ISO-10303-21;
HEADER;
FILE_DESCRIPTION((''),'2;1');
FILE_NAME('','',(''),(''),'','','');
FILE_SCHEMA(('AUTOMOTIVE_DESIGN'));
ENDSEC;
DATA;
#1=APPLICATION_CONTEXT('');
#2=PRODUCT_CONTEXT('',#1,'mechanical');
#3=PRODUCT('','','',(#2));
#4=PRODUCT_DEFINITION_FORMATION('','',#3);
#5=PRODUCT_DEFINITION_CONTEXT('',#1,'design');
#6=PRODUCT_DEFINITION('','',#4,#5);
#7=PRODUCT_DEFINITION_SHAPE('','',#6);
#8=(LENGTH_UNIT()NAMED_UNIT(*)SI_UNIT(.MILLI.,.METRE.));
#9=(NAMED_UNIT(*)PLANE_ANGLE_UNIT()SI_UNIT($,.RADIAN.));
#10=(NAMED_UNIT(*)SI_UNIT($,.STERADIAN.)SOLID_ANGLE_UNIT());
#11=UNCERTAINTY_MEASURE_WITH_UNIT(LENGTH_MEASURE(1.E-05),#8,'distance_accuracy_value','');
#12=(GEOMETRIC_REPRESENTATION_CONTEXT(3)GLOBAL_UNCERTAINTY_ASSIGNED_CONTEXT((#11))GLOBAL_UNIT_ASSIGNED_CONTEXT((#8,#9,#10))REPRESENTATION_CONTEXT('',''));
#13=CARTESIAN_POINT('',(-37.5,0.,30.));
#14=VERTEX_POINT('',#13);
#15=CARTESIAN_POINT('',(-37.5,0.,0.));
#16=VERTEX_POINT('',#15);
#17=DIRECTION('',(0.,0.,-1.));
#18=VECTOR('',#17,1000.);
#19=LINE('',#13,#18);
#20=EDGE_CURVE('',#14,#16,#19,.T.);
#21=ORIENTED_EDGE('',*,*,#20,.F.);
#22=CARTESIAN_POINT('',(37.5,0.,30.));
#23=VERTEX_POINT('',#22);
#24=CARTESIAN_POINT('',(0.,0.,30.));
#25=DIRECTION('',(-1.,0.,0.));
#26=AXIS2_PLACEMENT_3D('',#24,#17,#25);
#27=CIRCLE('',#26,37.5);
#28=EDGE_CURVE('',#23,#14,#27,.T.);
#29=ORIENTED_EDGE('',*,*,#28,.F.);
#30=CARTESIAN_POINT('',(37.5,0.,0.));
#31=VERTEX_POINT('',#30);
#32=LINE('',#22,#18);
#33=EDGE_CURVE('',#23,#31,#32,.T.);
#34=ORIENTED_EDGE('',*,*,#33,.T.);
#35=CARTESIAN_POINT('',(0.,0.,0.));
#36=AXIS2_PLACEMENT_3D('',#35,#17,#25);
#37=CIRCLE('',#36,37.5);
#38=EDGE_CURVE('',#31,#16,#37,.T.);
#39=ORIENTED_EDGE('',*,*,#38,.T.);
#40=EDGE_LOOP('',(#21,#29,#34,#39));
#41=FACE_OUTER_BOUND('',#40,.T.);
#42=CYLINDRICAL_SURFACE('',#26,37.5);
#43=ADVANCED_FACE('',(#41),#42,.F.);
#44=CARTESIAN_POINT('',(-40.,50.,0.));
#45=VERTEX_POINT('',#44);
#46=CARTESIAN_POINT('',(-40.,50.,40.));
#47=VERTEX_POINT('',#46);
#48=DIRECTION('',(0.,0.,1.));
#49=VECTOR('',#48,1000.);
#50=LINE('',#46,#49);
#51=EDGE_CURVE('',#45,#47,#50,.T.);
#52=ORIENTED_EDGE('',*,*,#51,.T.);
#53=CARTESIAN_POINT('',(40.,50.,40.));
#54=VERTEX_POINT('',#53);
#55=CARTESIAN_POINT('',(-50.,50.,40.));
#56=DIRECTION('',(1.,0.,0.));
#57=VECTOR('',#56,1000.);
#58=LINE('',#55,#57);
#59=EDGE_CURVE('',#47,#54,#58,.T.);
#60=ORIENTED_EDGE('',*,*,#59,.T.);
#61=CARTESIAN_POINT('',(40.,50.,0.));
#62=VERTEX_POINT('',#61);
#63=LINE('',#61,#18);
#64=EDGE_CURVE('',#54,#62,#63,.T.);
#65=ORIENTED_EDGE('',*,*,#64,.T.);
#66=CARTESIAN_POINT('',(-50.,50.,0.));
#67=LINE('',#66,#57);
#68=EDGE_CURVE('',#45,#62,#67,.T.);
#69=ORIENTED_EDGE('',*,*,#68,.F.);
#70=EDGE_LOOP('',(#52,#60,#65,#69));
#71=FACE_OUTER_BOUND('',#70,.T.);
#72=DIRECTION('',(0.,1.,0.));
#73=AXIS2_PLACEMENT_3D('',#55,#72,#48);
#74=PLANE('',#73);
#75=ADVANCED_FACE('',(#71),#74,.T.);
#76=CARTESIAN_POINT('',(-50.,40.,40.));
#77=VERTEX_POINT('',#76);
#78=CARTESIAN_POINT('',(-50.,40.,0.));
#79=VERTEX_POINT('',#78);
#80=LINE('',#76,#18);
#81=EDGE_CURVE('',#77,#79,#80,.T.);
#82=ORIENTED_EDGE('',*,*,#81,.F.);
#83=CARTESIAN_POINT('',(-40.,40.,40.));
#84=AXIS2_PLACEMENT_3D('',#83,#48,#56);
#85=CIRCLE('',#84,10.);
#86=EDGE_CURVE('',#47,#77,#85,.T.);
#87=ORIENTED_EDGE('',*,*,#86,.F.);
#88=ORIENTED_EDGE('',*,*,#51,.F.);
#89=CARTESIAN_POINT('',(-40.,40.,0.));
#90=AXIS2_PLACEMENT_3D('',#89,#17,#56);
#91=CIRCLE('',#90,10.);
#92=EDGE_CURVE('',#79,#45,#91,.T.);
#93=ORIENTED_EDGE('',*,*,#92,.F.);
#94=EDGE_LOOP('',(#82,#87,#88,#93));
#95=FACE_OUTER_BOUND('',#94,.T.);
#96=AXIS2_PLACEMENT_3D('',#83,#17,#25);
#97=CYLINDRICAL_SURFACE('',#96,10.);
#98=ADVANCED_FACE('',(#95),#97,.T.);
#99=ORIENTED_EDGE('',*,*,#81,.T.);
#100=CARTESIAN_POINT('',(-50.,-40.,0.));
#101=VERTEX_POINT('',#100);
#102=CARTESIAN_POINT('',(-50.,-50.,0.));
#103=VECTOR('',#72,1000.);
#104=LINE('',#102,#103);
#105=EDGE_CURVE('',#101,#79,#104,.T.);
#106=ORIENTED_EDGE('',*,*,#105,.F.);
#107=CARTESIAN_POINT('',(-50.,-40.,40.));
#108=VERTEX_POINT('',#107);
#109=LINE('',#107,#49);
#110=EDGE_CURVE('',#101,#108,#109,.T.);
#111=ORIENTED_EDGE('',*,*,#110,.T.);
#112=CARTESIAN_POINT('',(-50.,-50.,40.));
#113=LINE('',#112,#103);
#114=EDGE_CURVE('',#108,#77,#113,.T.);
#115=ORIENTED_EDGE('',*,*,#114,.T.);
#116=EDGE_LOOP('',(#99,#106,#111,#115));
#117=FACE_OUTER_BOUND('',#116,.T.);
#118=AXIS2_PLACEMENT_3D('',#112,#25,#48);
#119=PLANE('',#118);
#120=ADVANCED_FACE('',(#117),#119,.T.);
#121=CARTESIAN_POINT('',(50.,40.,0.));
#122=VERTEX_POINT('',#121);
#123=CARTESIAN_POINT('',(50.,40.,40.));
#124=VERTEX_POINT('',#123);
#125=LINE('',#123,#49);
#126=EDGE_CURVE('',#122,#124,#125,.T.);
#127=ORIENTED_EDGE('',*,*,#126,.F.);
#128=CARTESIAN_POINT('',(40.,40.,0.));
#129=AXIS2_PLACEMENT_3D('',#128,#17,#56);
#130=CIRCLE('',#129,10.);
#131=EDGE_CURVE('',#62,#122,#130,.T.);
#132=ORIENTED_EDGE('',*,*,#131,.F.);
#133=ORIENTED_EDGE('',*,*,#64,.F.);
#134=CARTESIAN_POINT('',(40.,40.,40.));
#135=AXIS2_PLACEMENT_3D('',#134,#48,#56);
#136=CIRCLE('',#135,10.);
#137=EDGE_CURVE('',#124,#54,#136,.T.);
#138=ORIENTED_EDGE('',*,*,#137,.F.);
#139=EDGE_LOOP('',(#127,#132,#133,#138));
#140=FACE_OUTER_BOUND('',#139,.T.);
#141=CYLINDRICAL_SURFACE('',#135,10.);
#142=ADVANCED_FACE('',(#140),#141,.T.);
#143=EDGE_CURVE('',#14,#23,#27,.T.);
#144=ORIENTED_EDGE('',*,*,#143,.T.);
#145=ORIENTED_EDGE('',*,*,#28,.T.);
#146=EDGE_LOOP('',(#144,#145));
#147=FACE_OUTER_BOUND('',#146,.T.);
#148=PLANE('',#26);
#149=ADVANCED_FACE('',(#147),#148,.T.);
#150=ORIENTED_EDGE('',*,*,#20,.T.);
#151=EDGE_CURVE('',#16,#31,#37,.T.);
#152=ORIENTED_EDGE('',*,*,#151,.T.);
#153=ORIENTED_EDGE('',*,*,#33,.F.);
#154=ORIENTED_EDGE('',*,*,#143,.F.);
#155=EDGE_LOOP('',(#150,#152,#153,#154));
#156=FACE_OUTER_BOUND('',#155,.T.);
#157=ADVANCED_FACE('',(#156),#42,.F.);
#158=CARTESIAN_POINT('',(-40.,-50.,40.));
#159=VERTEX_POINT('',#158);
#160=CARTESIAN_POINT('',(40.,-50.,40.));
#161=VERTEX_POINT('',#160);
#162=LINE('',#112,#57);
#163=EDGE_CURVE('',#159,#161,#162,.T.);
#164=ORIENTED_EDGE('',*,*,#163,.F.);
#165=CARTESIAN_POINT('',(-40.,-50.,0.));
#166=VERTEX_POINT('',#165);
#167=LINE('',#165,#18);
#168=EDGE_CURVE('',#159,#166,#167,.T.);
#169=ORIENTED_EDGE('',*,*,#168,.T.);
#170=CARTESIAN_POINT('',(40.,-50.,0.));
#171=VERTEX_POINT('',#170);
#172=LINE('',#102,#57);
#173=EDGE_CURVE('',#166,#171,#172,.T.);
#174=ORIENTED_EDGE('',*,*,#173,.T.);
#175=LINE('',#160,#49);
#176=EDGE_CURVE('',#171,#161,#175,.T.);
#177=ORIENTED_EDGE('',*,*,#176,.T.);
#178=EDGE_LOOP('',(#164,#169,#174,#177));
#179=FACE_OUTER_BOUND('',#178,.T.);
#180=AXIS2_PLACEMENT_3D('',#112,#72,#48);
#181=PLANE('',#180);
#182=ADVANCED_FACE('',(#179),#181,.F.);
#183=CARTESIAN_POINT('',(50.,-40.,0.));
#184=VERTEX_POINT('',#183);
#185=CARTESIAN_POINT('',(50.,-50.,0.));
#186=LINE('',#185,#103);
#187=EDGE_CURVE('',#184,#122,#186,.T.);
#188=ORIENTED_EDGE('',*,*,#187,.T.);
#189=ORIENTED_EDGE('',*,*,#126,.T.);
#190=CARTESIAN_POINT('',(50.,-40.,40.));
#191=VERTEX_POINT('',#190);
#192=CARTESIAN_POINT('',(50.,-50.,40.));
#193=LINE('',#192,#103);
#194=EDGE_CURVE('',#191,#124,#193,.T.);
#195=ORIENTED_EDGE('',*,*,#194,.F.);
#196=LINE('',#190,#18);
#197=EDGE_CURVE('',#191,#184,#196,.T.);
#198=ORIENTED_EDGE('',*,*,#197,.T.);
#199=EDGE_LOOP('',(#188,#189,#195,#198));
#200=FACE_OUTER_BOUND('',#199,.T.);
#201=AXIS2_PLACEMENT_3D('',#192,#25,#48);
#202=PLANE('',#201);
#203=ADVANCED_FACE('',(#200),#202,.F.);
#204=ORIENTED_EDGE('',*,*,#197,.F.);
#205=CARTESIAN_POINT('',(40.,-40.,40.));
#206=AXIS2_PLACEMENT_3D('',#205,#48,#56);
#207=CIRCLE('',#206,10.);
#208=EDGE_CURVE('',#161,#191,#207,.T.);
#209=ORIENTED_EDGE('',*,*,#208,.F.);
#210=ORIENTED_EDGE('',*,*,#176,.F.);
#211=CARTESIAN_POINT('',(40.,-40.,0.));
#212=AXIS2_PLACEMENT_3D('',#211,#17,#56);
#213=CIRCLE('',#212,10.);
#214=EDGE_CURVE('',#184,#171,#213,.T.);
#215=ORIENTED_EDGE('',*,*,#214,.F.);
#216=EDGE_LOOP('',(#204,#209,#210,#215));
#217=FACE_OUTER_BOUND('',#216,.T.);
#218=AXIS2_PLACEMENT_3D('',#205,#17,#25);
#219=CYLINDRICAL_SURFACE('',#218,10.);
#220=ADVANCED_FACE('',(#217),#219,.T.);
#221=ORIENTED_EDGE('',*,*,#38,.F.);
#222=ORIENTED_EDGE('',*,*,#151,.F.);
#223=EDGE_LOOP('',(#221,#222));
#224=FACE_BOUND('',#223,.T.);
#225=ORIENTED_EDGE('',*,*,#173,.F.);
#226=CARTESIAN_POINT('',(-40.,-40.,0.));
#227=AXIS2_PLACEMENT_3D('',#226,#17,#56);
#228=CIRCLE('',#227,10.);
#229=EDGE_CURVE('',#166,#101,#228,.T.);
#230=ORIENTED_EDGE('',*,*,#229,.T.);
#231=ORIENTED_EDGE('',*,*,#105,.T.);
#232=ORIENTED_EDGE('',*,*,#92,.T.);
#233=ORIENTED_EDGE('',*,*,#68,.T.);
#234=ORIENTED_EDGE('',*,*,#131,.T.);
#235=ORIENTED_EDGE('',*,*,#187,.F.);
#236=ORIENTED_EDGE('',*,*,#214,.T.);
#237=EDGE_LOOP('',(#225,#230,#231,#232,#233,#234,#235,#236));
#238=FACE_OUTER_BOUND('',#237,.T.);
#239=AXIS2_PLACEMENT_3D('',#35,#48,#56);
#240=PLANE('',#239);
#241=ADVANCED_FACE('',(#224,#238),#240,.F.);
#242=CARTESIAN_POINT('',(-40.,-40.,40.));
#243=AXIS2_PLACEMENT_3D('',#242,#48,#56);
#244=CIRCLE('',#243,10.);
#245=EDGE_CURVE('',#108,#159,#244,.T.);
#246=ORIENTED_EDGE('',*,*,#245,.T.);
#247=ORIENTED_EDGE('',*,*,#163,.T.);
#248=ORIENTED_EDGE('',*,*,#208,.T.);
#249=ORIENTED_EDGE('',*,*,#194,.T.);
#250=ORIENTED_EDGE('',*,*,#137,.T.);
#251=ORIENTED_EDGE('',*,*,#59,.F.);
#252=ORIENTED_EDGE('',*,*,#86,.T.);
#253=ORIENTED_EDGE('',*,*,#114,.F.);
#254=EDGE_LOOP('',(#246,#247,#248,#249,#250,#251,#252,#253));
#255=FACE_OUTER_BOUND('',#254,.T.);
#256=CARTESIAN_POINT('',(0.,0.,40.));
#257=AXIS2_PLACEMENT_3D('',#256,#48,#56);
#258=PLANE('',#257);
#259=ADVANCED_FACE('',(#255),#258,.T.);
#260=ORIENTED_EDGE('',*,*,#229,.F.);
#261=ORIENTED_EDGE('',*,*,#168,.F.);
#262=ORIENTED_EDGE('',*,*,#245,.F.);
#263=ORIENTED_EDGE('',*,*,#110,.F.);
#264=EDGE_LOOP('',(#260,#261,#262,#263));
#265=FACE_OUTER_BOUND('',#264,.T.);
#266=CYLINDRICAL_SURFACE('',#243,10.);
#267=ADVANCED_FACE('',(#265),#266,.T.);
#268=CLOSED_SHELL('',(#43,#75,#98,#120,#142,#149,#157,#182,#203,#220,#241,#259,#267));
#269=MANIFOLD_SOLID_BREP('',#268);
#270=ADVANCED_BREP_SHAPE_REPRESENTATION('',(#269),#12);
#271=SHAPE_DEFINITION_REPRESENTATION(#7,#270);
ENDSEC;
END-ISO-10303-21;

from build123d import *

# Parameters (mm, degrees)
SKETCH_1_W          = 100
SKETCH_1_H          = 100
EXTRUDE_1_DEPTH     = 40
SKETCH_2_R          = 37.5
CUT_EXTRUDE_1_DEPTH = 30
FILLET_1_R          = 10


with BuildPart() as part:
    # 草图1 → 凸台-拉伸1 (new body)
    with BuildSketch(Plane.XY):
        Rectangle(SKETCH_1_W, SKETCH_1_H)
    extrude(amount=EXTRUDE_1_DEPTH)

    # 草图2 → 切除-拉伸1 (cut)
    with BuildSketch(Plane(origin=(0, 0, 0), x_dir=(-1, 0, 0), z_dir=(0, 0, -1))):
        Circle(SKETCH_2_R)
    extrude(amount=-CUT_EXTRUDE_1_DEPTH, mode=Mode.SUBTRACT)

    # 圆角1
    fillet_1_edges = [part.edges().sort_by_distance(p)[0] for p in [
        (-50, -50, 20),
        (-50, 50, 20),
        (50, 50, 20),
        (50, -50, 20),
    ]]
    fillet(fillet_1_edges, radius=FILLET_1_R)


solid = part.part
